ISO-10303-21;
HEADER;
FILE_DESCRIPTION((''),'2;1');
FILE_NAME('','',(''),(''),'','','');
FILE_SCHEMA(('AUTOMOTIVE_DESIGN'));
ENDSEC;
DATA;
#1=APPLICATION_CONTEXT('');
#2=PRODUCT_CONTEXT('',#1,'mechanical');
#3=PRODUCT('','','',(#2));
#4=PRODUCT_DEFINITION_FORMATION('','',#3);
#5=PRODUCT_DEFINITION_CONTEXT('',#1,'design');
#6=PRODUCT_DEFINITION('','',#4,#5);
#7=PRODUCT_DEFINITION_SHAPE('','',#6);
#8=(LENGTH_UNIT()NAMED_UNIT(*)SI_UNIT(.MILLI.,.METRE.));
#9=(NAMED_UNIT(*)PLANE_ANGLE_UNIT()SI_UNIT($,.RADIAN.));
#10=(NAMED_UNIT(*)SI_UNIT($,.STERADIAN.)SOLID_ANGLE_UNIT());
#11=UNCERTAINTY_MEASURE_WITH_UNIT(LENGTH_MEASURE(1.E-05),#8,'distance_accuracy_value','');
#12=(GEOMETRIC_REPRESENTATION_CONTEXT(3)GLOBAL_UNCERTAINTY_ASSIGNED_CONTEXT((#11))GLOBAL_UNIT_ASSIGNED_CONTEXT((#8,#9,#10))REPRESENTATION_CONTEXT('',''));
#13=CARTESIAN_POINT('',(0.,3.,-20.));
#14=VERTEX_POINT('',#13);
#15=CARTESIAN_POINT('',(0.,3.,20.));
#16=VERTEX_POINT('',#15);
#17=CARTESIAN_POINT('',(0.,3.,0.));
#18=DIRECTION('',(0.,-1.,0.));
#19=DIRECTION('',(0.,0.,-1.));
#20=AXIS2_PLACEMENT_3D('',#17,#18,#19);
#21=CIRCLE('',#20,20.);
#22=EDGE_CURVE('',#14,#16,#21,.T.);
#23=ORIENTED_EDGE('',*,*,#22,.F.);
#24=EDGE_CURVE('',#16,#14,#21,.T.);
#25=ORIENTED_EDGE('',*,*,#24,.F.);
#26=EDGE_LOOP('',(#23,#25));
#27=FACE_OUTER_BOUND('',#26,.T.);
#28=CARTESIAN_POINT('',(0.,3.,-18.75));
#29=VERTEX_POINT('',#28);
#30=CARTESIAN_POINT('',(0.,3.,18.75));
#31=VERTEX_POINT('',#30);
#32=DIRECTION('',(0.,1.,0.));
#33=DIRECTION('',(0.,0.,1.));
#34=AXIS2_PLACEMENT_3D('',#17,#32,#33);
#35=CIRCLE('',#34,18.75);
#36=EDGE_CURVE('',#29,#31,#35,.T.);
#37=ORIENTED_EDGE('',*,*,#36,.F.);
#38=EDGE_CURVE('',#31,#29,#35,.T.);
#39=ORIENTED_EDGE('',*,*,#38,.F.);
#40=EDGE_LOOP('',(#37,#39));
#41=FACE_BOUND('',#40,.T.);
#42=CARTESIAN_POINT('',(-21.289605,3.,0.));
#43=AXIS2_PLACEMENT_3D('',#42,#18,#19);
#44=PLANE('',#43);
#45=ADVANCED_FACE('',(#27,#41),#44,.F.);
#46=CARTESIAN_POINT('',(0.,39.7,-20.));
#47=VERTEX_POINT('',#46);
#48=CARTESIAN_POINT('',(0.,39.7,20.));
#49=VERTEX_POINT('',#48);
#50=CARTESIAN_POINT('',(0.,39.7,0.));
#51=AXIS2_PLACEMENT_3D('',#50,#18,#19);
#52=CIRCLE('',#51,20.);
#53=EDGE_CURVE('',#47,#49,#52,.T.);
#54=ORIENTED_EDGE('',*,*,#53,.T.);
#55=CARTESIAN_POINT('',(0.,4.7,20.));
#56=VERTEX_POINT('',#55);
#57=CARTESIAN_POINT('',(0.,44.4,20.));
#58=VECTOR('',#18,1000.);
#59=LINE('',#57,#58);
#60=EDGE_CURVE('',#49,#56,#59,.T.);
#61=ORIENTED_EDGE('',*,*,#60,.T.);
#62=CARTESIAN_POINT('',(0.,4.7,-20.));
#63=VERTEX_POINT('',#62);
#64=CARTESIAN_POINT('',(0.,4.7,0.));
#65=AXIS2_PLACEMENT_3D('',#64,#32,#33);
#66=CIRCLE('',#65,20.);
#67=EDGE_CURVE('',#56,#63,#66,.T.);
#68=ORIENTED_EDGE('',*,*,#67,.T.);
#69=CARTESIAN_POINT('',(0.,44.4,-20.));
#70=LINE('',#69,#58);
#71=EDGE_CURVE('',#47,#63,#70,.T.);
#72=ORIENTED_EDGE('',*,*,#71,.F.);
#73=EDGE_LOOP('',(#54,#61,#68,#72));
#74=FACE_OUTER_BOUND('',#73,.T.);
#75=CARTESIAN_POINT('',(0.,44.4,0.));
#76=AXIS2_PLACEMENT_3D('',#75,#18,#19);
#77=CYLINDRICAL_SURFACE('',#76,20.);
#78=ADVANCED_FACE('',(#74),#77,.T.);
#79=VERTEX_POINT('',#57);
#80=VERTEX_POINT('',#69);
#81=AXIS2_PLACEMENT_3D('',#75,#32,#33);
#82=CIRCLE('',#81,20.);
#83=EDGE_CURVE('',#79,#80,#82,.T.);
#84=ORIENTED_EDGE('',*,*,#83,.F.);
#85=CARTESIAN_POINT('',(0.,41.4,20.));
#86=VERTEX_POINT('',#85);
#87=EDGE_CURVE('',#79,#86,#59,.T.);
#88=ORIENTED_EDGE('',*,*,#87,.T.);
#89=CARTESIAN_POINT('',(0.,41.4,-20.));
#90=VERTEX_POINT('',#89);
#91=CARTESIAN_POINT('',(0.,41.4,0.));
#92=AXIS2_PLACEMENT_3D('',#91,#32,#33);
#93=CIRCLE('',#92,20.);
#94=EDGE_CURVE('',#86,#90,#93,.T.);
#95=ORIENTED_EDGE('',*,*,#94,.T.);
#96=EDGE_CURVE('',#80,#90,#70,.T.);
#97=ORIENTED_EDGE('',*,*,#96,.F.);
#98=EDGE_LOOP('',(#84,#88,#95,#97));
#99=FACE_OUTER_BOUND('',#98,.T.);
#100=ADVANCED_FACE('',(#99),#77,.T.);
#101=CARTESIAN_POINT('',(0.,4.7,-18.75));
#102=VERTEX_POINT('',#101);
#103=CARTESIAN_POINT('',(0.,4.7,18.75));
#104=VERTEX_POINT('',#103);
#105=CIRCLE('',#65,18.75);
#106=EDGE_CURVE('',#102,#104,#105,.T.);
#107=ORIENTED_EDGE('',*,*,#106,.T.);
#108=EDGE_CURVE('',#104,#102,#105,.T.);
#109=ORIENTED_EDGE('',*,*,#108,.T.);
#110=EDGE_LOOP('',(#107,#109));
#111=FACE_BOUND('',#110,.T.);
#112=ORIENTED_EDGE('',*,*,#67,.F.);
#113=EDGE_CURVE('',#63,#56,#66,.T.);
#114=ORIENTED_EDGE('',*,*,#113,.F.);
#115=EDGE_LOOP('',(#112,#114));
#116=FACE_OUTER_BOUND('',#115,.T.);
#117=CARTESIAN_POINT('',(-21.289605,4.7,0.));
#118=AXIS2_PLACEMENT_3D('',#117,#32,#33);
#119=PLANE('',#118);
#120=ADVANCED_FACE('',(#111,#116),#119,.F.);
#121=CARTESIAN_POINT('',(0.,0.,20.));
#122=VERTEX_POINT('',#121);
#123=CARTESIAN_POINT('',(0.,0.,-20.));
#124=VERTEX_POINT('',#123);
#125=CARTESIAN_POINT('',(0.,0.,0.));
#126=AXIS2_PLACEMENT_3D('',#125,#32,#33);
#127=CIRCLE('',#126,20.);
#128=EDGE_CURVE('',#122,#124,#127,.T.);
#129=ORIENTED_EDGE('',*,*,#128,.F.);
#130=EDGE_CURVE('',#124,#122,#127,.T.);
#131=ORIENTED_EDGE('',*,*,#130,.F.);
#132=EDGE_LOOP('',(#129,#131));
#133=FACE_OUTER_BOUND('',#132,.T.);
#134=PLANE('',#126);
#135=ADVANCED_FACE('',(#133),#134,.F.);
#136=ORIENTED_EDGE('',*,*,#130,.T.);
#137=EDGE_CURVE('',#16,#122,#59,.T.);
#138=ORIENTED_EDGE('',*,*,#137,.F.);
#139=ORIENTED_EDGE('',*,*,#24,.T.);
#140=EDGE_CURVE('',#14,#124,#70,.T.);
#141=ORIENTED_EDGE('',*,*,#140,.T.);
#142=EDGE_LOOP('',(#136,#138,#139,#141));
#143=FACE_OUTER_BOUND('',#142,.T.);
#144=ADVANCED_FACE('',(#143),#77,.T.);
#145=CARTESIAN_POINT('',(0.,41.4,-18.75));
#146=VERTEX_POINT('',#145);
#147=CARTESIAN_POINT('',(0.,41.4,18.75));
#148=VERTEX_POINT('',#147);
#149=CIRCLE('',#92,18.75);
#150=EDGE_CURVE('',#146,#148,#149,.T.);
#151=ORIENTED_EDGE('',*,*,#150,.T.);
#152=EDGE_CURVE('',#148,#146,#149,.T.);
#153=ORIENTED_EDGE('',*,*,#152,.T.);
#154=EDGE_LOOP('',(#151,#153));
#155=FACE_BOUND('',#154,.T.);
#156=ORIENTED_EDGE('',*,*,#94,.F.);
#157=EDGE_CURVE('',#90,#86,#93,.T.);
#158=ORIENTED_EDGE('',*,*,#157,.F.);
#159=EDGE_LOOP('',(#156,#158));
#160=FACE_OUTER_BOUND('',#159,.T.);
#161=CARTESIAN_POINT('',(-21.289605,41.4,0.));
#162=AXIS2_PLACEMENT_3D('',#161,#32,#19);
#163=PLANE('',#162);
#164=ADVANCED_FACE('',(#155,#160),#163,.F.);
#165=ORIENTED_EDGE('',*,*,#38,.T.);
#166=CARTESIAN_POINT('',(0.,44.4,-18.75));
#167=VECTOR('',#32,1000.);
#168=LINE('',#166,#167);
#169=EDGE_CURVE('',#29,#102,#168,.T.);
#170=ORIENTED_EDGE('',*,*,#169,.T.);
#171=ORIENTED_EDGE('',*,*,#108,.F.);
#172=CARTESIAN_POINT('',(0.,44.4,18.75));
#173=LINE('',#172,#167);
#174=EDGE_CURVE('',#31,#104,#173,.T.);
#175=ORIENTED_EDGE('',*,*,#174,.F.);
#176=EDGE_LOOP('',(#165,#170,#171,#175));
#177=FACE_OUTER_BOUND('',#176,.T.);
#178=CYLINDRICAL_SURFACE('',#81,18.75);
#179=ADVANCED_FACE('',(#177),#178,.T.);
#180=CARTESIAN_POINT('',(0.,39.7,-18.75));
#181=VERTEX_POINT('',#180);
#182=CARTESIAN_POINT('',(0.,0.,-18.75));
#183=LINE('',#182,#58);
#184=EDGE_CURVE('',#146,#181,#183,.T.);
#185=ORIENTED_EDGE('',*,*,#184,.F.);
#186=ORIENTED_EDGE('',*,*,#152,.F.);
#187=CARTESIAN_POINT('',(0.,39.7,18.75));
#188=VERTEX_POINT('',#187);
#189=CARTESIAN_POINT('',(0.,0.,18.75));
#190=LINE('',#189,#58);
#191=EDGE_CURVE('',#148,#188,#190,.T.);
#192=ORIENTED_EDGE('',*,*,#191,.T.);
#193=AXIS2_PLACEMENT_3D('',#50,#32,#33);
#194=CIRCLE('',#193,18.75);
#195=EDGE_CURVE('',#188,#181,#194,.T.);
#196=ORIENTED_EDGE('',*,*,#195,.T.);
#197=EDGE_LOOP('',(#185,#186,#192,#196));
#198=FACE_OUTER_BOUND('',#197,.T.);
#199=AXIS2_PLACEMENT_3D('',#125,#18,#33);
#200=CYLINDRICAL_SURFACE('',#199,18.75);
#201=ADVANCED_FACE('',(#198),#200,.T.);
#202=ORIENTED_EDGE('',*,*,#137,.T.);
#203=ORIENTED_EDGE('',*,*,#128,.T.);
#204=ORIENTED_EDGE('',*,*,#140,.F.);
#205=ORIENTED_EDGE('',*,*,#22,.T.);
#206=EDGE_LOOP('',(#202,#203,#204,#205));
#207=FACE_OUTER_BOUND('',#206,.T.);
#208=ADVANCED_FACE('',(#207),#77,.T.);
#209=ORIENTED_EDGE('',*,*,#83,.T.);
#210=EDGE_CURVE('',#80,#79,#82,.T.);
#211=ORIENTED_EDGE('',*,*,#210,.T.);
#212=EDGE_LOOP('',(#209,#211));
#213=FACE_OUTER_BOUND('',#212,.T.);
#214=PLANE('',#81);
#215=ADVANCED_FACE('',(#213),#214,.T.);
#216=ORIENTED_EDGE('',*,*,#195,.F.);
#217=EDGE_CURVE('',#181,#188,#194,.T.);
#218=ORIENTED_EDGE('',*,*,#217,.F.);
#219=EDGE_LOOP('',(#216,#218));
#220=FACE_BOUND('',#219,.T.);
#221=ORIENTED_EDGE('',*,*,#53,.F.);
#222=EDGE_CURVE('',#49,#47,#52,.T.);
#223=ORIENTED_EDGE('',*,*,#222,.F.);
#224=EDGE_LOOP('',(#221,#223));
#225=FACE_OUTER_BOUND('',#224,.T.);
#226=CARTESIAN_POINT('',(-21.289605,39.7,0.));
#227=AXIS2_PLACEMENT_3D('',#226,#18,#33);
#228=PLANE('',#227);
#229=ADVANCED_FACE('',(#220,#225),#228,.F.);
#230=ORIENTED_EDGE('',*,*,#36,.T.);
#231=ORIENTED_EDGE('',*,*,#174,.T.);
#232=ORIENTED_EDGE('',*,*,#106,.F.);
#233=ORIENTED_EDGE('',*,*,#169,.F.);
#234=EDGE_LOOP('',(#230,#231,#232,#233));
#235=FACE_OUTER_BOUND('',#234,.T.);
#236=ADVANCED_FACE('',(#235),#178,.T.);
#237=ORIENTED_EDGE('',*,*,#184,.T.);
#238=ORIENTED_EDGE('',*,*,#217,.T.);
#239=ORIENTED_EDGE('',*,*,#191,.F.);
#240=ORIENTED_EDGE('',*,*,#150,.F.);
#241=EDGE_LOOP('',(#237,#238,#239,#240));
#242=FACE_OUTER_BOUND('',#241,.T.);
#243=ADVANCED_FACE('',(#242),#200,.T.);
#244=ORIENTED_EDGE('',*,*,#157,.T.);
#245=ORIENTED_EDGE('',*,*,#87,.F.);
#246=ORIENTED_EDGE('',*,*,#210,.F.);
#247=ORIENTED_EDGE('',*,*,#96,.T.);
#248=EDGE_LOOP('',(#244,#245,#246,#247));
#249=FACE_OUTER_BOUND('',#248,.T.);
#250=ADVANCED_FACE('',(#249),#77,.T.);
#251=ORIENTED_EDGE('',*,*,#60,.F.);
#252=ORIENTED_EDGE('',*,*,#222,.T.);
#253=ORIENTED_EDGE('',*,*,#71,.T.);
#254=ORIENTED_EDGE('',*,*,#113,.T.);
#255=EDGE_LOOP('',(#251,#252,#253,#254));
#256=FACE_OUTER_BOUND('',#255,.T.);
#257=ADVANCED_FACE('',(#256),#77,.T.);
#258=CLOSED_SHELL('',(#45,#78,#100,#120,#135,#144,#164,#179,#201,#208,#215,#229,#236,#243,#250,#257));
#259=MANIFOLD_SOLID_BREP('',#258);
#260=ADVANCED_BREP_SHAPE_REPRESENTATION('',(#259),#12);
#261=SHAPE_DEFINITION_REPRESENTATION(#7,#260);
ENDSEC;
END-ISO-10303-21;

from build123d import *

# Parameters (mm, degrees)
SKETCH_1_R      = 20
EXTRUDE_1_DEPTH = 44.4
SKETCH_2_W      = 2.53960462
SKETCH_2_H      = 1.7


with BuildPart() as part:
    # 草图1 → 凸台-拉伸1 (new body)
    with BuildSketch(Plane(origin=(0, 0, 0), x_dir=(1, 0, 0), z_dir=(0, 1, 0))):
        with Locations(Location((0, 0, 0), (0, 0, 270))):
            Circle(SKETCH_1_R)
    extrude(amount=EXTRUDE_1_DEPTH)

    # 草图2 → 切除-旋转1 (revolve, cut)
    with BuildSketch(Plane.XY, mode=Mode.PRIVATE) as cut_revolve_1_sk:
        with Locations((-20.01980231, 3.85)):
            Rectangle(SKETCH_2_W, SKETCH_2_H)
    cut_revolve_1 = revolve(cut_revolve_1_sk.sketch.rotate(Axis((0, 44.4, 0), (0, -1, 0)), 270), axis=Axis((0, 44.4, 0), (0, -1, 0)), mode=Mode.SUBTRACT)

    # 镜向1: 切除-旋转1 across plane
    add(cut_revolve_1.mirror(Plane(origin=(0, 22.2, 0), x_dir=(0, 0, 1), z_dir=(0, -1, 0))), mode=Mode.SUBTRACT)


solid = part.part
